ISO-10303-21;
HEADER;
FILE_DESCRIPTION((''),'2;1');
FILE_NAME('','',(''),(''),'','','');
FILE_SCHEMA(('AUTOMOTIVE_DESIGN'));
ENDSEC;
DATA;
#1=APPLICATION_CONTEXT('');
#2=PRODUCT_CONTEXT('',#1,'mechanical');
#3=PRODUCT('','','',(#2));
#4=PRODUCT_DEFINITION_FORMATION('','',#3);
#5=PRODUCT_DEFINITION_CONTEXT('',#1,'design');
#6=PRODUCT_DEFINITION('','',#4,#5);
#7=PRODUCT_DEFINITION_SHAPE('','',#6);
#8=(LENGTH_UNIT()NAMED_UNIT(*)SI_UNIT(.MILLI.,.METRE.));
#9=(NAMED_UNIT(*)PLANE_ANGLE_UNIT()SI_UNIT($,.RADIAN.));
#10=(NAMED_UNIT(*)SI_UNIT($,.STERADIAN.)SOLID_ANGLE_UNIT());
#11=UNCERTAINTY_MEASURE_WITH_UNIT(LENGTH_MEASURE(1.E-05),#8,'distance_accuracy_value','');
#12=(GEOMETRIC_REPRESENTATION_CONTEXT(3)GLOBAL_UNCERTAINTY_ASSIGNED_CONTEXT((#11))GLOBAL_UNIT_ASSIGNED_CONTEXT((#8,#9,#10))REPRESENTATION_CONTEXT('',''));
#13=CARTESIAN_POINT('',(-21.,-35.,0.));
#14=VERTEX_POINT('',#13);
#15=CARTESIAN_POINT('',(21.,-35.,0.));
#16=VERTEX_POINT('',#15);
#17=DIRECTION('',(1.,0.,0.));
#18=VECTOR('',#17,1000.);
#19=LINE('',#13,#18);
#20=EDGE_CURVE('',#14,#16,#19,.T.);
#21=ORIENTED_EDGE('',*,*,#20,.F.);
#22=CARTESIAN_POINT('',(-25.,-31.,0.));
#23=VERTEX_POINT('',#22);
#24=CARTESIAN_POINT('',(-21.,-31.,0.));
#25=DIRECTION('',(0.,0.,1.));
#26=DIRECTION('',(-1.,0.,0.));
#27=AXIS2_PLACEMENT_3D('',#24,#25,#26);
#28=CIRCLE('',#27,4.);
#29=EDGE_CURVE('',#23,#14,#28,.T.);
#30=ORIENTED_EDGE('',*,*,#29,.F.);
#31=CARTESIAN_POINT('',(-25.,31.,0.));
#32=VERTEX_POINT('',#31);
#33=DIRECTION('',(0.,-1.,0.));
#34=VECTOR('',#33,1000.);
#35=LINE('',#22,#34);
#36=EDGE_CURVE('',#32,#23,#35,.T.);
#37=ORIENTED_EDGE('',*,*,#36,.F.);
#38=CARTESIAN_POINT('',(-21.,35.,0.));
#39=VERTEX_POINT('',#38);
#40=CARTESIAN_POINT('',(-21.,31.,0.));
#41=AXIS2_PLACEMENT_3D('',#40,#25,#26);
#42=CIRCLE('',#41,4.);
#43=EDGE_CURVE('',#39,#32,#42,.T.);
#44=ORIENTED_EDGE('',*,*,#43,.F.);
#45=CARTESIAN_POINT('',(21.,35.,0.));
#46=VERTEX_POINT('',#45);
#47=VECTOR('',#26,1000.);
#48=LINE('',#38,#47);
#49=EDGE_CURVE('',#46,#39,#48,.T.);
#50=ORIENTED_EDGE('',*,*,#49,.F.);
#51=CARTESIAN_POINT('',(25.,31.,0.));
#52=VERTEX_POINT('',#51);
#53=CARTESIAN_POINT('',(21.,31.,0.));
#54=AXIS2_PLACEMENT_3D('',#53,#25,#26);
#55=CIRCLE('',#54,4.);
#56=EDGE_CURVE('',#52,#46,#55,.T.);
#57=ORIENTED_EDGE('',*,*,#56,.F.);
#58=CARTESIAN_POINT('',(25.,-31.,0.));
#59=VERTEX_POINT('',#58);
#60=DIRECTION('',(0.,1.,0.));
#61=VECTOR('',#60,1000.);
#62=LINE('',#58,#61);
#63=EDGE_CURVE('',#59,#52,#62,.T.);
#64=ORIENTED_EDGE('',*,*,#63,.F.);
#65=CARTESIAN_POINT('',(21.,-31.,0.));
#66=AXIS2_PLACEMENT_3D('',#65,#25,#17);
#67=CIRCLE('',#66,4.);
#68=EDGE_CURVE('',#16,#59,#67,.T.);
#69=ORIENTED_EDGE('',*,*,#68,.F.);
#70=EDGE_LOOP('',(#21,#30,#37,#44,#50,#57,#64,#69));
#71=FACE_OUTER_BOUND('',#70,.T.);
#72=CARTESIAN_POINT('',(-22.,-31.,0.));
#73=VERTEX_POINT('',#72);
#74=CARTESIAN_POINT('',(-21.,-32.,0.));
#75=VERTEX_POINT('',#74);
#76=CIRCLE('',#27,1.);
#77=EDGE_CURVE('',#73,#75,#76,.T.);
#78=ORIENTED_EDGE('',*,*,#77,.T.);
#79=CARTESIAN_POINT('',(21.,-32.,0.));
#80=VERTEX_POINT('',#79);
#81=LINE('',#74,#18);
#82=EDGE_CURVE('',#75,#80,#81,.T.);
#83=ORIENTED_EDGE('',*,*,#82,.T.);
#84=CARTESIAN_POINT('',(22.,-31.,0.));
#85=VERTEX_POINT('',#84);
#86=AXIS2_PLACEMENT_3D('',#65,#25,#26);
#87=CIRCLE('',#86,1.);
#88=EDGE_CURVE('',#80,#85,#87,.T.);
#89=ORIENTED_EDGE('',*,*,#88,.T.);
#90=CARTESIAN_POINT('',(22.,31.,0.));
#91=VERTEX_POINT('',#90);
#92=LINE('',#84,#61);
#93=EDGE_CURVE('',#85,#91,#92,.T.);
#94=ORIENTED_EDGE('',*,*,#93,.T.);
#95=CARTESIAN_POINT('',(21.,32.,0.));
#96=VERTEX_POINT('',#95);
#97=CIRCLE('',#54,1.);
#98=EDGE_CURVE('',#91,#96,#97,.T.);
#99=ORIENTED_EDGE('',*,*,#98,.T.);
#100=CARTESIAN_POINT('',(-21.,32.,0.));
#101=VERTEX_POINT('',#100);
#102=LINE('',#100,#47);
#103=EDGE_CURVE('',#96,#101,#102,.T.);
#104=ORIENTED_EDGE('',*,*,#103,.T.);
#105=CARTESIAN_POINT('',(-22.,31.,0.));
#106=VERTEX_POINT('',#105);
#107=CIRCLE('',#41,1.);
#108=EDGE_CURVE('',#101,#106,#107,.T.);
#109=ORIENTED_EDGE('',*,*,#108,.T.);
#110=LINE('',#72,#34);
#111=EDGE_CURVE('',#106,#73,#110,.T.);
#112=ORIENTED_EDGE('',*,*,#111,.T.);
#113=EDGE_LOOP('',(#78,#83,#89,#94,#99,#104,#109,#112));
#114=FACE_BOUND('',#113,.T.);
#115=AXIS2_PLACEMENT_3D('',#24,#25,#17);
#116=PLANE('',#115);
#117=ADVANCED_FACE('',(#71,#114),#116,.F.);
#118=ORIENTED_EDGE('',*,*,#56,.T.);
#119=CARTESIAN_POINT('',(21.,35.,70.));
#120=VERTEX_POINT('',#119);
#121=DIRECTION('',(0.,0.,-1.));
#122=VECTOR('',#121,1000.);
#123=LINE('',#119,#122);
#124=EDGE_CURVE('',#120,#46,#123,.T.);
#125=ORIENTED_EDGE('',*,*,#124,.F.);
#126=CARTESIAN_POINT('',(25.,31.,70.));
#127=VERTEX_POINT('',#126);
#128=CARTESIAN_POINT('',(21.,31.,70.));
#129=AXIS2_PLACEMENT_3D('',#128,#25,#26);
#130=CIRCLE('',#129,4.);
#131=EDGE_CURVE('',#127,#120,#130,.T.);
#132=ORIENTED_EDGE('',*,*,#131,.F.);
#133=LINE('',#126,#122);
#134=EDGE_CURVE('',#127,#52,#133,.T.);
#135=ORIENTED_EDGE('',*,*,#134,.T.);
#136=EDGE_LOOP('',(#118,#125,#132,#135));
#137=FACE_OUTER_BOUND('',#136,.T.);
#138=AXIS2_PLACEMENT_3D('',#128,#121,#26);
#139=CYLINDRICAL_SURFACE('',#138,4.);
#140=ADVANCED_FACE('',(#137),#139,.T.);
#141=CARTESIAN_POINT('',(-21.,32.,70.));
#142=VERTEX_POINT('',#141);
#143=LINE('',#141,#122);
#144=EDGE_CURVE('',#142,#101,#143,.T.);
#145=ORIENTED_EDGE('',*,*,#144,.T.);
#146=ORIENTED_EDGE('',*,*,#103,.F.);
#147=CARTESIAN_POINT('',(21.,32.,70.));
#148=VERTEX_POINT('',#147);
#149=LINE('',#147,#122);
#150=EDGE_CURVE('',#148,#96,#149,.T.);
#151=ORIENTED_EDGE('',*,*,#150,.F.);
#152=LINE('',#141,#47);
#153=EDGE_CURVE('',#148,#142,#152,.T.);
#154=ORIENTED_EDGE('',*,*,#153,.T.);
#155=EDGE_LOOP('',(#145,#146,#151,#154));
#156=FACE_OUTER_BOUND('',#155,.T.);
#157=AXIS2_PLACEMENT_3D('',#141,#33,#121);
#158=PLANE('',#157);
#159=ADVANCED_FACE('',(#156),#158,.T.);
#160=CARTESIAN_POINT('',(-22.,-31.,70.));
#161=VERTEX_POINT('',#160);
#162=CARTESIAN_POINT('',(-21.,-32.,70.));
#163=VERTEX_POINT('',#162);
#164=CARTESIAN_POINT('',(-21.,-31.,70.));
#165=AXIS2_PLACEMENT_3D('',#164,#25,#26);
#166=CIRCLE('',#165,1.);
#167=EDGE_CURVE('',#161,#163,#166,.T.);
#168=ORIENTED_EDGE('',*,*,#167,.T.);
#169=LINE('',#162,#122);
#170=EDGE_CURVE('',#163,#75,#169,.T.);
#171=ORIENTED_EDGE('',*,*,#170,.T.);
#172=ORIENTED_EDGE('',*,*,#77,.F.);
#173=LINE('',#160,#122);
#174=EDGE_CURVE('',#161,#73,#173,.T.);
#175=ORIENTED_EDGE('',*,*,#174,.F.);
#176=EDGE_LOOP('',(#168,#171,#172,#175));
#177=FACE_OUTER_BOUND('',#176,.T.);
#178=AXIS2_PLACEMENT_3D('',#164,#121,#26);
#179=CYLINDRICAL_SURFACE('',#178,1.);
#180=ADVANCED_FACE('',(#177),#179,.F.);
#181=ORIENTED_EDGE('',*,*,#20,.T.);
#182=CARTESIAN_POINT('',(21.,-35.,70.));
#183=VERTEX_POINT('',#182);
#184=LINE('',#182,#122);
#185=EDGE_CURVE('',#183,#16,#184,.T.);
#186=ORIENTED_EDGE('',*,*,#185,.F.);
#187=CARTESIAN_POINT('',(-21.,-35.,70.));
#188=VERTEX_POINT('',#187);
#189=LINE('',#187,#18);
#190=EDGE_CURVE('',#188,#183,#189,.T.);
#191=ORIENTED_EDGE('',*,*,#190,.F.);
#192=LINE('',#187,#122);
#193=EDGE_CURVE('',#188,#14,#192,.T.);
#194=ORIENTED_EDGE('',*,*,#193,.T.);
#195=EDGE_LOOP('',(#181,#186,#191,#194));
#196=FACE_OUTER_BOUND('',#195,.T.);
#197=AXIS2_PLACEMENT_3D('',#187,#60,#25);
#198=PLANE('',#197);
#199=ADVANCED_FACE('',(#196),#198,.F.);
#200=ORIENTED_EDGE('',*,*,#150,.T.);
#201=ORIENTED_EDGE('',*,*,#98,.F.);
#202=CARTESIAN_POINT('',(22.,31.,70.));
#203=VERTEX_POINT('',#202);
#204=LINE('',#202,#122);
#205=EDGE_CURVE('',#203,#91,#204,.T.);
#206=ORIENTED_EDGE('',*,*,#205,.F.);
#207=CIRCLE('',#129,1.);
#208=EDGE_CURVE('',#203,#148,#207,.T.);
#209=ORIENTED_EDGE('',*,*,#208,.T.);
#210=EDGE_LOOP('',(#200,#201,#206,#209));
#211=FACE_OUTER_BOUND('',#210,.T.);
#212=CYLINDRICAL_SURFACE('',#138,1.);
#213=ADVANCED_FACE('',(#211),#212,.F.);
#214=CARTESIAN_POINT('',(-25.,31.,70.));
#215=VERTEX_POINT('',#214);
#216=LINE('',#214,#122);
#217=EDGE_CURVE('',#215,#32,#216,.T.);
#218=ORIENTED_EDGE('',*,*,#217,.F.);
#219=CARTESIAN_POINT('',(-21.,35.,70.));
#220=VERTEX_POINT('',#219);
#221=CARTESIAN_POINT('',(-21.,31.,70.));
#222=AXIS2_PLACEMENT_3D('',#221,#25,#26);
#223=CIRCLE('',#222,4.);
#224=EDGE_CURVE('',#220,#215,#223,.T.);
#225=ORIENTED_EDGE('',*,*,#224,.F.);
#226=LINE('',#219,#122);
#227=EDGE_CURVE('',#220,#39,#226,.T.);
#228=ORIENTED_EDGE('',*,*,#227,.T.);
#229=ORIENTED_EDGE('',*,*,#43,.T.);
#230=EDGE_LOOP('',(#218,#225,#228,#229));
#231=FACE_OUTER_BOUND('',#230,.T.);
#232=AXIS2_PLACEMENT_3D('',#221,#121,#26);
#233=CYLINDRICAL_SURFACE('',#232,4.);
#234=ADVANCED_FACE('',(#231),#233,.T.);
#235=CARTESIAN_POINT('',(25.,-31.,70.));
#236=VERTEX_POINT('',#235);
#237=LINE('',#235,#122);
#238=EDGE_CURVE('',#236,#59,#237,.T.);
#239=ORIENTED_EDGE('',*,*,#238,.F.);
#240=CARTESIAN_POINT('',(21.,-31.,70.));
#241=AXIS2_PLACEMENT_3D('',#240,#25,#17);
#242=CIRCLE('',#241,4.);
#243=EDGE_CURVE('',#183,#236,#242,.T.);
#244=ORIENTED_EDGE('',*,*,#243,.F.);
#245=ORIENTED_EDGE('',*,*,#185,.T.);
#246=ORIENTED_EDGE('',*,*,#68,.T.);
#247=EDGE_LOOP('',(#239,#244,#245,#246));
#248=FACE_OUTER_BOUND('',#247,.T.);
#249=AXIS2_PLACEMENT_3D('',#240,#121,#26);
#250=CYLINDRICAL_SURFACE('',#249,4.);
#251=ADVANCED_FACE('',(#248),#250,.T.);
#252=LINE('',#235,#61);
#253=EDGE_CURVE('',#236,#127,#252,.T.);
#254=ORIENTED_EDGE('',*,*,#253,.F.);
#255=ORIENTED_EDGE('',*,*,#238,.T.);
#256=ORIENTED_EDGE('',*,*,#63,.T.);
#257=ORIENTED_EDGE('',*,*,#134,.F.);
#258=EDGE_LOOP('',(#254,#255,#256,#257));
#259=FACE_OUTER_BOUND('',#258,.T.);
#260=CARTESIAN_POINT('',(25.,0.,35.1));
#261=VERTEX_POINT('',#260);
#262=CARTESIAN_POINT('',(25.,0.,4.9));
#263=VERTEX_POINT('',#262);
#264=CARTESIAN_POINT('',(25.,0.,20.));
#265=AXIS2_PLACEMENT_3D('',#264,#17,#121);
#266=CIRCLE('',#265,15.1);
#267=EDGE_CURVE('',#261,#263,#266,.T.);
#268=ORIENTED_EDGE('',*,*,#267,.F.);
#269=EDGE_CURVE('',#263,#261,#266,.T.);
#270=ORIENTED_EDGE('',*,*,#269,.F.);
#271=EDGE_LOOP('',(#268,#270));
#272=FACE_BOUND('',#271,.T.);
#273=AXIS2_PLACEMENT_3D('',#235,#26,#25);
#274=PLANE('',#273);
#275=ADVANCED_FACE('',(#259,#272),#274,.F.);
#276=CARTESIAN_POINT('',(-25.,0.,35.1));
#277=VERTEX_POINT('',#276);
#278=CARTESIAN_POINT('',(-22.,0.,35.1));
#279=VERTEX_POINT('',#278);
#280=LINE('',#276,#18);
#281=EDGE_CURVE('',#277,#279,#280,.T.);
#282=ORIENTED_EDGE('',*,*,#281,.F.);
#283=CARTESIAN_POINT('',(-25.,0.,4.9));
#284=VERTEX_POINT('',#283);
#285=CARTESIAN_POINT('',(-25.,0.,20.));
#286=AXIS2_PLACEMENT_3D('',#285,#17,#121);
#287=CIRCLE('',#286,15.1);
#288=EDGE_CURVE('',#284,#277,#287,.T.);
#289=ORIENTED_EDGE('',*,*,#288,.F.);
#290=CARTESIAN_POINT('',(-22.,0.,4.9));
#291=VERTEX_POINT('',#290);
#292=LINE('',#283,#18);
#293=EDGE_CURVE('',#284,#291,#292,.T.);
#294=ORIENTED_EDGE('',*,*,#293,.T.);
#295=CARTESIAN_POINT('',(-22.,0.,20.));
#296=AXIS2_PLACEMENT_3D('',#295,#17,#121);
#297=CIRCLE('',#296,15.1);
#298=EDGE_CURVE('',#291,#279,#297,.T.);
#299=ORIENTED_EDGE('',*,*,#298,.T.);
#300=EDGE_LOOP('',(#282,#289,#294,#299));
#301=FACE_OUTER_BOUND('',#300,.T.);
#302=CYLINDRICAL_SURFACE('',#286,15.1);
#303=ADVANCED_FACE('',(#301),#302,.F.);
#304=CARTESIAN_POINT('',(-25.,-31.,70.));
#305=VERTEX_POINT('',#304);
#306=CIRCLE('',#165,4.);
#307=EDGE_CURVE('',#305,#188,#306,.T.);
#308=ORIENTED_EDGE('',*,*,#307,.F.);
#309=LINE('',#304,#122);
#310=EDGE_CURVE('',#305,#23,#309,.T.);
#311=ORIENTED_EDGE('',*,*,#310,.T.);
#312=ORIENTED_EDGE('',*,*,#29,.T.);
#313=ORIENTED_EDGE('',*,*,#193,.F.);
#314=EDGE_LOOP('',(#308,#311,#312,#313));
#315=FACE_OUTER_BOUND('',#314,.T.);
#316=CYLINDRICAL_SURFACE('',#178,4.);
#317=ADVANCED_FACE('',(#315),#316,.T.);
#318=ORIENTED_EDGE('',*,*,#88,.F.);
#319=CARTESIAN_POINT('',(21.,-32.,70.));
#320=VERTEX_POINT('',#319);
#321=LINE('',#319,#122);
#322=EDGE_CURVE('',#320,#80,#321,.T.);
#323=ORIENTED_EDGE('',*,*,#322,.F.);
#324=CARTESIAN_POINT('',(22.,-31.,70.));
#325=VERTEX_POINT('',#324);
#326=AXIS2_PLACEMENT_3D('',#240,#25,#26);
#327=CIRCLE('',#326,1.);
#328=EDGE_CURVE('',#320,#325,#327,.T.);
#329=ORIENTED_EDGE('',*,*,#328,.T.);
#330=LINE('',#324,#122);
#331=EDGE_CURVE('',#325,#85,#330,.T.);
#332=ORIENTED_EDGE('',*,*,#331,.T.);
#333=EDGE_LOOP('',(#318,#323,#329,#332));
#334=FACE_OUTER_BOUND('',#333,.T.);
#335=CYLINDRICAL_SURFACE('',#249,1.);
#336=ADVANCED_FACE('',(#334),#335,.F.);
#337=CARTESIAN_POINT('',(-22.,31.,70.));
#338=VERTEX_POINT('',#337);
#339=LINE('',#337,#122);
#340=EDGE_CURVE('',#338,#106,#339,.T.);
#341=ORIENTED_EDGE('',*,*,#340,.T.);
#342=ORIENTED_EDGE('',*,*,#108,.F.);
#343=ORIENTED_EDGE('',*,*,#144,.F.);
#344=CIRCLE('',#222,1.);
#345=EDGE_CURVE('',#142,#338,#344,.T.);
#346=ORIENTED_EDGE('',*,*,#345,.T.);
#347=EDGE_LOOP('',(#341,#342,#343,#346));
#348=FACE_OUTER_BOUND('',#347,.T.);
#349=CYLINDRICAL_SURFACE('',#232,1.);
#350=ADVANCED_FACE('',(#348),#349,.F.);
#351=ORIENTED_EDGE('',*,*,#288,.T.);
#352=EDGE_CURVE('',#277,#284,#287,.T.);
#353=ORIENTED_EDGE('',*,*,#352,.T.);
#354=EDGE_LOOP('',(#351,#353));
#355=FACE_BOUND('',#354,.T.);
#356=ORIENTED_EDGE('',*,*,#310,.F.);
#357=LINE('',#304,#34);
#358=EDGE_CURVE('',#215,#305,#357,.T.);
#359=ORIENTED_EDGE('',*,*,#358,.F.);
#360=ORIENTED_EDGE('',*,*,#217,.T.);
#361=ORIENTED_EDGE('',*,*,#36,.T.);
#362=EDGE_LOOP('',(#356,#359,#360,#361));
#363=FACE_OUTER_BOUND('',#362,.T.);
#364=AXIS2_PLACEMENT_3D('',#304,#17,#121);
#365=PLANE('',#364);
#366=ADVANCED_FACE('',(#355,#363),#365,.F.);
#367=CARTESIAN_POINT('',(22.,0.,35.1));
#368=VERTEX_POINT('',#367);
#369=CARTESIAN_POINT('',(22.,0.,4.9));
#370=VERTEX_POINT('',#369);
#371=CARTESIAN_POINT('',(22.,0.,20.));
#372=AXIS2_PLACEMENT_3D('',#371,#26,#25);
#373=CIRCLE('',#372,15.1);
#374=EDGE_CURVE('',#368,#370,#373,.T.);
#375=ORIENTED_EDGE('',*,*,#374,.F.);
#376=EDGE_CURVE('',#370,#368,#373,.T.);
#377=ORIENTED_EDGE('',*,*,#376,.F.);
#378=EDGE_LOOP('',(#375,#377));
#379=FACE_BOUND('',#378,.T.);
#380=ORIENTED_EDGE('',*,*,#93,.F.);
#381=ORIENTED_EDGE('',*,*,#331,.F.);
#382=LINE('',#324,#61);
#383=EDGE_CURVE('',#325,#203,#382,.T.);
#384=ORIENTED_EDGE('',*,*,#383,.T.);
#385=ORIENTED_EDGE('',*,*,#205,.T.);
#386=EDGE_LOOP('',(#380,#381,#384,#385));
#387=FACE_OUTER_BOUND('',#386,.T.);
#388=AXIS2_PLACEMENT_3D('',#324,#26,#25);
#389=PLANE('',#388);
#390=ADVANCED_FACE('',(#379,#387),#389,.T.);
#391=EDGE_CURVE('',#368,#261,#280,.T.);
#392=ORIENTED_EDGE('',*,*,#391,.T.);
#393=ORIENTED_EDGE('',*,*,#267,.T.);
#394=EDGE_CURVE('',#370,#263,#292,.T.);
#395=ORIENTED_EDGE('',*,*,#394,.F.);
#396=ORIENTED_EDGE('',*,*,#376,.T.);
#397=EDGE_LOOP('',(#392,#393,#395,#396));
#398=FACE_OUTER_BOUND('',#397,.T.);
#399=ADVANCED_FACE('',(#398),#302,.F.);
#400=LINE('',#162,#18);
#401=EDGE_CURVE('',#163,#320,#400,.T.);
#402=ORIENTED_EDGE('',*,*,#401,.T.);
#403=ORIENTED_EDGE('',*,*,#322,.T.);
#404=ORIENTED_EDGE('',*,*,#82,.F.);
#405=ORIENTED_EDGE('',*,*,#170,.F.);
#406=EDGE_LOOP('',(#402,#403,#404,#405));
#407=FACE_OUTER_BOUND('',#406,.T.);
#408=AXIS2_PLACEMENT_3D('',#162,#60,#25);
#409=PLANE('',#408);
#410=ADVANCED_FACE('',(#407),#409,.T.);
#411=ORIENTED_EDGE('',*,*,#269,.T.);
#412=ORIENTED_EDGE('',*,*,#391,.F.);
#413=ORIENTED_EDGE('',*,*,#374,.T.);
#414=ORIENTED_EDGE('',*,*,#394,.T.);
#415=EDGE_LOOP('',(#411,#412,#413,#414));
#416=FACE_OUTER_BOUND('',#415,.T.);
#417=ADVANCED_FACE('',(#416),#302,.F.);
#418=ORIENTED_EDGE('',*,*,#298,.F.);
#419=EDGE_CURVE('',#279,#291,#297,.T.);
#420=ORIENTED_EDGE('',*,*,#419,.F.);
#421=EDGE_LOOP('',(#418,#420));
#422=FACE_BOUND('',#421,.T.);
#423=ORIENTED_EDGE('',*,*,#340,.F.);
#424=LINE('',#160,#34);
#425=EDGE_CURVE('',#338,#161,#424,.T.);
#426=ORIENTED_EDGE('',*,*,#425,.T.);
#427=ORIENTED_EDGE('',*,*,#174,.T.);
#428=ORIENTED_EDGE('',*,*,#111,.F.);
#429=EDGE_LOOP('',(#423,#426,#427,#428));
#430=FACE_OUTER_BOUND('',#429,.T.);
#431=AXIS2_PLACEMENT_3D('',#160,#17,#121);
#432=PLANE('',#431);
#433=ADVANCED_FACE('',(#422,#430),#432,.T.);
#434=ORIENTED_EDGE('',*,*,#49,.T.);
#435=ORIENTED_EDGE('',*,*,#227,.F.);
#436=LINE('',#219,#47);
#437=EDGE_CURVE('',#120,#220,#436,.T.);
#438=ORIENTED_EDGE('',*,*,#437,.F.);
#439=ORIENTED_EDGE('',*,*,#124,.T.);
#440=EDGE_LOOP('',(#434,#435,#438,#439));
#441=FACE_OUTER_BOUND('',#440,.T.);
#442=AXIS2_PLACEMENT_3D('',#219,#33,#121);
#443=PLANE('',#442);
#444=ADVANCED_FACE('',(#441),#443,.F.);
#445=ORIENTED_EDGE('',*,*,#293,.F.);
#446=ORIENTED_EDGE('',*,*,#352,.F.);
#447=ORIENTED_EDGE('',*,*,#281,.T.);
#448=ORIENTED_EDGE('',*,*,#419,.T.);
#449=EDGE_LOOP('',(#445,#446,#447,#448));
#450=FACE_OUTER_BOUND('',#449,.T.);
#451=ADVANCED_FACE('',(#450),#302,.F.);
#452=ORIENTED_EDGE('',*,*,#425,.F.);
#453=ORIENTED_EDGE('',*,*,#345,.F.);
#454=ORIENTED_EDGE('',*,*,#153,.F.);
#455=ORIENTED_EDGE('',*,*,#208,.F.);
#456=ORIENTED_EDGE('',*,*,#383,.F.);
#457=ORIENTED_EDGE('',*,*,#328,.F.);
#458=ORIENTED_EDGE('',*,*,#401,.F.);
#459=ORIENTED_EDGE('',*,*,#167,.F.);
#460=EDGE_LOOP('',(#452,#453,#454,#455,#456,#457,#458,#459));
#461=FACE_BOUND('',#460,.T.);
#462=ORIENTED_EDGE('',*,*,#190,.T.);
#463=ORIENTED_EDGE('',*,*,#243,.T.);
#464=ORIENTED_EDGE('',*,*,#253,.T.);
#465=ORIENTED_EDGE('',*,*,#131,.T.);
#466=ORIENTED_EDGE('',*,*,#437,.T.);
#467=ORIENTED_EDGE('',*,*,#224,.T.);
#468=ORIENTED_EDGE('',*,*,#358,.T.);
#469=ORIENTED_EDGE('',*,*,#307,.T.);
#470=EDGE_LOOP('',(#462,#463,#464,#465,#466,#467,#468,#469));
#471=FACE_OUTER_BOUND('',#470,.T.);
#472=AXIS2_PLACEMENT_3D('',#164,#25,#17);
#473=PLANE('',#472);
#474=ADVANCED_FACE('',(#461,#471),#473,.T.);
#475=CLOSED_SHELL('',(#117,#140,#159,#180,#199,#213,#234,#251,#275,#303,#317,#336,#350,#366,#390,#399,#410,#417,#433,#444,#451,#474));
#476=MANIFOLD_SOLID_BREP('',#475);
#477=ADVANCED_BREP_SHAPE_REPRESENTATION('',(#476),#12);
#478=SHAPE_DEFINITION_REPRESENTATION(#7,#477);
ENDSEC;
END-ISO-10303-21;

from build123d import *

# Parameters (mm, degrees)
EXTRUDE_THIN1_DEPTH = 70
SKETCH2_R           = 15.1
CUT_EXTRUDE1_DEPTH  = 93.870878105


with BuildPart() as part:
    # Sketch1 → Extrude-Thin1 (new body)
    with BuildSketch(Plane.XY):
        with BuildLine():
            Line((-25, 31), (-25, -31))
            ThreePointArc((-25, -31), (-23.828427125, -33.828427125), (-21, -35))
            Line((-21, -35), (21, -35))
            ThreePointArc((21, -35), (23.828427125, -33.828427125), (25, -31))
            Line((25, -31), (25, 31))
            ThreePointArc((25, 31), (23.828427125, 33.828427125), (21, 35))
            Line((21, 35), (-21, 35))
            ThreePointArc((-21, 35), (-23.828427125, 33.828427125), (-25, 31))
        make_face()
        with BuildLine():
            Line((-22, 31), (-22, -31))
            ThreePointArc((-22, -31), (-21.707106781, -31.707106781), (-21, -32))
            Line((-21, -32), (21, -32))
            ThreePointArc((21, -32), (21.707106781, -31.707106781), (22, -31))
            Line((22, -31), (22, 31))
            ThreePointArc((22, 31), (21.707106781, 31.707106781), (21, 32))
            Line((21, 32), (-21, 32))
            ThreePointArc((-21, 32), (-21.707106781, 31.707106781), (-22, 31))
        make_face(mode=Mode.SUBTRACT)
    extrude(amount=EXTRUDE_THIN1_DEPTH)

    # Sketch2 → Cut-Extrude1 (cut, through all)
    with BuildSketch(Plane(origin=(25, 0, 0), x_dir=(0, 0, -1), z_dir=(1, 0, 0))):
        with Locations((-20, 0)):
            Circle(SKETCH2_R)
    extrude(amount=-CUT_EXTRUDE1_DEPTH, mode=Mode.SUBTRACT)


solid = part.part
